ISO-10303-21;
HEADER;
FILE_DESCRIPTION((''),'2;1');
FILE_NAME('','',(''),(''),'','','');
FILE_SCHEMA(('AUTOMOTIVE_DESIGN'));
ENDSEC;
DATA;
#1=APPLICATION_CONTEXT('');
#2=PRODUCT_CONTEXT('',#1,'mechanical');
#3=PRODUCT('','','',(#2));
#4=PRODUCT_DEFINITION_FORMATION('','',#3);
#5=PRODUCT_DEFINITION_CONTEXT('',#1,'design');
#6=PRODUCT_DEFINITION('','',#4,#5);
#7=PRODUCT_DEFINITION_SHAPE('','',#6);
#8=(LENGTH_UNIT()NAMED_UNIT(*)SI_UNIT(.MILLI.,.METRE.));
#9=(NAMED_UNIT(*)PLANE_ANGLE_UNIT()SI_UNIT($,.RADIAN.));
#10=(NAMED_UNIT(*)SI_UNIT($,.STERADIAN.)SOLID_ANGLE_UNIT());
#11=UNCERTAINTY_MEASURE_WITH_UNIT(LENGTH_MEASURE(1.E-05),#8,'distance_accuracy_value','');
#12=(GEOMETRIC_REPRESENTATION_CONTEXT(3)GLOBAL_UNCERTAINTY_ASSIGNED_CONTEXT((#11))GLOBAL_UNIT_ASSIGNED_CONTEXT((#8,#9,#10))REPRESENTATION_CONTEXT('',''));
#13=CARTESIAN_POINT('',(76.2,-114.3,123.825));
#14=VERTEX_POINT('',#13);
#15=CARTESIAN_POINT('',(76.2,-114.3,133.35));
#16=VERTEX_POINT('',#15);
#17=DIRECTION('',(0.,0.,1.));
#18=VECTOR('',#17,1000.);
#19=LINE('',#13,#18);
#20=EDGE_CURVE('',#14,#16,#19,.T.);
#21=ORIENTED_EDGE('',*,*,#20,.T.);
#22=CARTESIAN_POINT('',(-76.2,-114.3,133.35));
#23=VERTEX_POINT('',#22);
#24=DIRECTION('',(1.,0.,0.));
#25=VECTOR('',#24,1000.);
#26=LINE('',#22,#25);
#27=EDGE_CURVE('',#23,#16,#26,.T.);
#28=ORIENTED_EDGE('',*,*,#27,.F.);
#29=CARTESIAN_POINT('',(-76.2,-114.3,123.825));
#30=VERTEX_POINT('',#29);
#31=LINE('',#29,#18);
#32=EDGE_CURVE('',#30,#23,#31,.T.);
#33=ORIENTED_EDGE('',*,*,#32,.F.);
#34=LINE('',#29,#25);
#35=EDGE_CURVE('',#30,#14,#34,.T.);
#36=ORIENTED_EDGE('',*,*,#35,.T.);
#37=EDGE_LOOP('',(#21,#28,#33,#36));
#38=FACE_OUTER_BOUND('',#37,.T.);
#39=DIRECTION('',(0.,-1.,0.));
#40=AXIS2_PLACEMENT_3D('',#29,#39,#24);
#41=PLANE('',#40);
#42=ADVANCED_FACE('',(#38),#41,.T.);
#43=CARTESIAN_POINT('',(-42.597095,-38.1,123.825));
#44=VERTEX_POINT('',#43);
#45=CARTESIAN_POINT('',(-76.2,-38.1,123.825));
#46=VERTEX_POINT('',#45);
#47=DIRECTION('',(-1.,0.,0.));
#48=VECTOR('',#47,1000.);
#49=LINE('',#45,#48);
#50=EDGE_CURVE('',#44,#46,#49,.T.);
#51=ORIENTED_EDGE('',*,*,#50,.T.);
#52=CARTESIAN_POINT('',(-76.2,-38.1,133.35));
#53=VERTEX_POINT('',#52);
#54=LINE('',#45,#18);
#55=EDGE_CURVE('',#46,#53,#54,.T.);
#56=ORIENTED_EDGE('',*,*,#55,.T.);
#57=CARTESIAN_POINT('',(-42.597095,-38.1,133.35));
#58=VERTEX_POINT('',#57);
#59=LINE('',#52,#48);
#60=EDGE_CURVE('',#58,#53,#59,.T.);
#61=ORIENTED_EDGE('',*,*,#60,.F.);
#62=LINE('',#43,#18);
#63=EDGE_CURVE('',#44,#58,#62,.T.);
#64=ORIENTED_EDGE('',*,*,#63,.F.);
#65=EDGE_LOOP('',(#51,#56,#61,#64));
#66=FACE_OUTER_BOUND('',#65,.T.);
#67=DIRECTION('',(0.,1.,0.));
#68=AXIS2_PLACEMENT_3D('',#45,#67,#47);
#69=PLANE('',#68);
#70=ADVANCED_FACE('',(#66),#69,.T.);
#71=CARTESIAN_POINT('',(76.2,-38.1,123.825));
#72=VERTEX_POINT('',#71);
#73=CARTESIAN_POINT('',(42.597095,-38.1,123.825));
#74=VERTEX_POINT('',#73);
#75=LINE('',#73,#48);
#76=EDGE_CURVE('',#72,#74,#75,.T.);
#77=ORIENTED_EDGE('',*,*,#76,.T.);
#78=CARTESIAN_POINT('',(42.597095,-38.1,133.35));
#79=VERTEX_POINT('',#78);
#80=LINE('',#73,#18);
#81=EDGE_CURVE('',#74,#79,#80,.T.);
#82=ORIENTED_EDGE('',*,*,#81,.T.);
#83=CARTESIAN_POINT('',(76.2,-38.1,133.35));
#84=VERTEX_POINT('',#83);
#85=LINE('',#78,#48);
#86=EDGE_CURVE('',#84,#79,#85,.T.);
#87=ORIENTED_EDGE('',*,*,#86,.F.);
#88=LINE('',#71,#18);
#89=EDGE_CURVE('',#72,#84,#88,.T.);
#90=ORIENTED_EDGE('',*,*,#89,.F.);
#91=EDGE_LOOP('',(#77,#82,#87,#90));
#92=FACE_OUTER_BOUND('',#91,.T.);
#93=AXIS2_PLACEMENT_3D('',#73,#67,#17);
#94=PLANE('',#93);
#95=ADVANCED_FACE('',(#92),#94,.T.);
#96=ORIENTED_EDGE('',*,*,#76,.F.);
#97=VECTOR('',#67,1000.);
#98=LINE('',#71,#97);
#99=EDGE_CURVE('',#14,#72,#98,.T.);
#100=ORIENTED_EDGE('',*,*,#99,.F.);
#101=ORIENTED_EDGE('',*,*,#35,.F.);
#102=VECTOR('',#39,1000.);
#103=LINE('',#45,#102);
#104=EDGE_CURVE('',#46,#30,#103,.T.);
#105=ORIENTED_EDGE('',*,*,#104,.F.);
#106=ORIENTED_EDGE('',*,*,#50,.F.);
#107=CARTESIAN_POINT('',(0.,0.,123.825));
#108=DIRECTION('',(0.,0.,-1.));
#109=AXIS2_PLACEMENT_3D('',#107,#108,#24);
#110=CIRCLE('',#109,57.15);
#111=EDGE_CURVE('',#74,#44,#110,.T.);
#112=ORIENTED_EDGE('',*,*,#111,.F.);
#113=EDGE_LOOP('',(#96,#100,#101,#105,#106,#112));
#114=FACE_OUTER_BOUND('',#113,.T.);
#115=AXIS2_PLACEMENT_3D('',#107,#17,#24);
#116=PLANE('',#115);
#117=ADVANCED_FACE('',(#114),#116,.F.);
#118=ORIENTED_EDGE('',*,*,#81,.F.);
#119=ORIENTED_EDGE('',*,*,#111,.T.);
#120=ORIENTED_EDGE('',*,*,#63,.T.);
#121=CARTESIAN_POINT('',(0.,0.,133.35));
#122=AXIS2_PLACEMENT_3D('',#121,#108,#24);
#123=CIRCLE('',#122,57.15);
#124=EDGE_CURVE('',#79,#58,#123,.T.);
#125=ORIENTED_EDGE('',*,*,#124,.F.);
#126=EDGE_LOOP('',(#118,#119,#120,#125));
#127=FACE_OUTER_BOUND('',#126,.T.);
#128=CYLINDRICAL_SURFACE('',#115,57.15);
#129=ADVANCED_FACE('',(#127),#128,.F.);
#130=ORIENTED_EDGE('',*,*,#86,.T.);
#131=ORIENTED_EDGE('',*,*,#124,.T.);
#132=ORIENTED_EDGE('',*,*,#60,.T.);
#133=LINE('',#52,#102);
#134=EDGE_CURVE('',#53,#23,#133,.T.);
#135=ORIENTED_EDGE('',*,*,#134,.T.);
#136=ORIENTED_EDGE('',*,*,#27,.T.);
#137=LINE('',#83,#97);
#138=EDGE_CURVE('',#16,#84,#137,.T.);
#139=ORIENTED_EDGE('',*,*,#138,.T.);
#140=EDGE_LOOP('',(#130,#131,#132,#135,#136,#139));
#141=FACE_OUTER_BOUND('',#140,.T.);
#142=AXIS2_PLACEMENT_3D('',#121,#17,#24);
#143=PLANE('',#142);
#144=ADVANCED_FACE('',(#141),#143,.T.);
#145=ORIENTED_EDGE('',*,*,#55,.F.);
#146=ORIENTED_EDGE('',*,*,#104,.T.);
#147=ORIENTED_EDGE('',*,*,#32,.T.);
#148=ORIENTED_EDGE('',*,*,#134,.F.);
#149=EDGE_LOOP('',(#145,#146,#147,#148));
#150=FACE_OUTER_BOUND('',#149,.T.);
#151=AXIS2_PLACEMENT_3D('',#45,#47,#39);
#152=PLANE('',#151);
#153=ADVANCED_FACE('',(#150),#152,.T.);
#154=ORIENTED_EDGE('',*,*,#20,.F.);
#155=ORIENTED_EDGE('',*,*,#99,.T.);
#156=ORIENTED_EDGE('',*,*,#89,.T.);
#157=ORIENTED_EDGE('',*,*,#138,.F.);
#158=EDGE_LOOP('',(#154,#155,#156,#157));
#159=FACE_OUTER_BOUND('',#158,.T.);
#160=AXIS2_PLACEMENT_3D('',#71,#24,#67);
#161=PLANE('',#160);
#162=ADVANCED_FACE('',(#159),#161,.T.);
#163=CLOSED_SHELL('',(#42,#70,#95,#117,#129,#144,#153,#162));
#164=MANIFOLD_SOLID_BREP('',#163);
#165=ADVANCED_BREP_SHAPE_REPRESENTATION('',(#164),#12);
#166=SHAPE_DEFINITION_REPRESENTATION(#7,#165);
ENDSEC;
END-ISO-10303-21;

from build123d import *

# Parameters (mm, degrees)
BOSS_EXTRUDE1_DEPTH = 9.525


with BuildPart() as part:
    # Sketch1 → Boss-Extrude1 (new body)
    with BuildSketch(Plane.XY.offset(133.35)):
        with BuildLine():
            Line((-76.2, -38.1), (-42.597094971, -38.1))
            ThreePointArc((-42.597094971, -38.1), (0, -57.15), (42.597094971, -38.1))
            Line((42.597094971, -38.1), (76.2, -38.1))
            Line((76.2, -38.1), (76.2, -114.3))
            Line((76.2, -114.3), (-76.2, -114.3))
            Line((-76.2, -114.3), (-76.2, -38.1))
        make_face()
    extrude(amount=-BOSS_EXTRUDE1_DEPTH)


solid = part.part
